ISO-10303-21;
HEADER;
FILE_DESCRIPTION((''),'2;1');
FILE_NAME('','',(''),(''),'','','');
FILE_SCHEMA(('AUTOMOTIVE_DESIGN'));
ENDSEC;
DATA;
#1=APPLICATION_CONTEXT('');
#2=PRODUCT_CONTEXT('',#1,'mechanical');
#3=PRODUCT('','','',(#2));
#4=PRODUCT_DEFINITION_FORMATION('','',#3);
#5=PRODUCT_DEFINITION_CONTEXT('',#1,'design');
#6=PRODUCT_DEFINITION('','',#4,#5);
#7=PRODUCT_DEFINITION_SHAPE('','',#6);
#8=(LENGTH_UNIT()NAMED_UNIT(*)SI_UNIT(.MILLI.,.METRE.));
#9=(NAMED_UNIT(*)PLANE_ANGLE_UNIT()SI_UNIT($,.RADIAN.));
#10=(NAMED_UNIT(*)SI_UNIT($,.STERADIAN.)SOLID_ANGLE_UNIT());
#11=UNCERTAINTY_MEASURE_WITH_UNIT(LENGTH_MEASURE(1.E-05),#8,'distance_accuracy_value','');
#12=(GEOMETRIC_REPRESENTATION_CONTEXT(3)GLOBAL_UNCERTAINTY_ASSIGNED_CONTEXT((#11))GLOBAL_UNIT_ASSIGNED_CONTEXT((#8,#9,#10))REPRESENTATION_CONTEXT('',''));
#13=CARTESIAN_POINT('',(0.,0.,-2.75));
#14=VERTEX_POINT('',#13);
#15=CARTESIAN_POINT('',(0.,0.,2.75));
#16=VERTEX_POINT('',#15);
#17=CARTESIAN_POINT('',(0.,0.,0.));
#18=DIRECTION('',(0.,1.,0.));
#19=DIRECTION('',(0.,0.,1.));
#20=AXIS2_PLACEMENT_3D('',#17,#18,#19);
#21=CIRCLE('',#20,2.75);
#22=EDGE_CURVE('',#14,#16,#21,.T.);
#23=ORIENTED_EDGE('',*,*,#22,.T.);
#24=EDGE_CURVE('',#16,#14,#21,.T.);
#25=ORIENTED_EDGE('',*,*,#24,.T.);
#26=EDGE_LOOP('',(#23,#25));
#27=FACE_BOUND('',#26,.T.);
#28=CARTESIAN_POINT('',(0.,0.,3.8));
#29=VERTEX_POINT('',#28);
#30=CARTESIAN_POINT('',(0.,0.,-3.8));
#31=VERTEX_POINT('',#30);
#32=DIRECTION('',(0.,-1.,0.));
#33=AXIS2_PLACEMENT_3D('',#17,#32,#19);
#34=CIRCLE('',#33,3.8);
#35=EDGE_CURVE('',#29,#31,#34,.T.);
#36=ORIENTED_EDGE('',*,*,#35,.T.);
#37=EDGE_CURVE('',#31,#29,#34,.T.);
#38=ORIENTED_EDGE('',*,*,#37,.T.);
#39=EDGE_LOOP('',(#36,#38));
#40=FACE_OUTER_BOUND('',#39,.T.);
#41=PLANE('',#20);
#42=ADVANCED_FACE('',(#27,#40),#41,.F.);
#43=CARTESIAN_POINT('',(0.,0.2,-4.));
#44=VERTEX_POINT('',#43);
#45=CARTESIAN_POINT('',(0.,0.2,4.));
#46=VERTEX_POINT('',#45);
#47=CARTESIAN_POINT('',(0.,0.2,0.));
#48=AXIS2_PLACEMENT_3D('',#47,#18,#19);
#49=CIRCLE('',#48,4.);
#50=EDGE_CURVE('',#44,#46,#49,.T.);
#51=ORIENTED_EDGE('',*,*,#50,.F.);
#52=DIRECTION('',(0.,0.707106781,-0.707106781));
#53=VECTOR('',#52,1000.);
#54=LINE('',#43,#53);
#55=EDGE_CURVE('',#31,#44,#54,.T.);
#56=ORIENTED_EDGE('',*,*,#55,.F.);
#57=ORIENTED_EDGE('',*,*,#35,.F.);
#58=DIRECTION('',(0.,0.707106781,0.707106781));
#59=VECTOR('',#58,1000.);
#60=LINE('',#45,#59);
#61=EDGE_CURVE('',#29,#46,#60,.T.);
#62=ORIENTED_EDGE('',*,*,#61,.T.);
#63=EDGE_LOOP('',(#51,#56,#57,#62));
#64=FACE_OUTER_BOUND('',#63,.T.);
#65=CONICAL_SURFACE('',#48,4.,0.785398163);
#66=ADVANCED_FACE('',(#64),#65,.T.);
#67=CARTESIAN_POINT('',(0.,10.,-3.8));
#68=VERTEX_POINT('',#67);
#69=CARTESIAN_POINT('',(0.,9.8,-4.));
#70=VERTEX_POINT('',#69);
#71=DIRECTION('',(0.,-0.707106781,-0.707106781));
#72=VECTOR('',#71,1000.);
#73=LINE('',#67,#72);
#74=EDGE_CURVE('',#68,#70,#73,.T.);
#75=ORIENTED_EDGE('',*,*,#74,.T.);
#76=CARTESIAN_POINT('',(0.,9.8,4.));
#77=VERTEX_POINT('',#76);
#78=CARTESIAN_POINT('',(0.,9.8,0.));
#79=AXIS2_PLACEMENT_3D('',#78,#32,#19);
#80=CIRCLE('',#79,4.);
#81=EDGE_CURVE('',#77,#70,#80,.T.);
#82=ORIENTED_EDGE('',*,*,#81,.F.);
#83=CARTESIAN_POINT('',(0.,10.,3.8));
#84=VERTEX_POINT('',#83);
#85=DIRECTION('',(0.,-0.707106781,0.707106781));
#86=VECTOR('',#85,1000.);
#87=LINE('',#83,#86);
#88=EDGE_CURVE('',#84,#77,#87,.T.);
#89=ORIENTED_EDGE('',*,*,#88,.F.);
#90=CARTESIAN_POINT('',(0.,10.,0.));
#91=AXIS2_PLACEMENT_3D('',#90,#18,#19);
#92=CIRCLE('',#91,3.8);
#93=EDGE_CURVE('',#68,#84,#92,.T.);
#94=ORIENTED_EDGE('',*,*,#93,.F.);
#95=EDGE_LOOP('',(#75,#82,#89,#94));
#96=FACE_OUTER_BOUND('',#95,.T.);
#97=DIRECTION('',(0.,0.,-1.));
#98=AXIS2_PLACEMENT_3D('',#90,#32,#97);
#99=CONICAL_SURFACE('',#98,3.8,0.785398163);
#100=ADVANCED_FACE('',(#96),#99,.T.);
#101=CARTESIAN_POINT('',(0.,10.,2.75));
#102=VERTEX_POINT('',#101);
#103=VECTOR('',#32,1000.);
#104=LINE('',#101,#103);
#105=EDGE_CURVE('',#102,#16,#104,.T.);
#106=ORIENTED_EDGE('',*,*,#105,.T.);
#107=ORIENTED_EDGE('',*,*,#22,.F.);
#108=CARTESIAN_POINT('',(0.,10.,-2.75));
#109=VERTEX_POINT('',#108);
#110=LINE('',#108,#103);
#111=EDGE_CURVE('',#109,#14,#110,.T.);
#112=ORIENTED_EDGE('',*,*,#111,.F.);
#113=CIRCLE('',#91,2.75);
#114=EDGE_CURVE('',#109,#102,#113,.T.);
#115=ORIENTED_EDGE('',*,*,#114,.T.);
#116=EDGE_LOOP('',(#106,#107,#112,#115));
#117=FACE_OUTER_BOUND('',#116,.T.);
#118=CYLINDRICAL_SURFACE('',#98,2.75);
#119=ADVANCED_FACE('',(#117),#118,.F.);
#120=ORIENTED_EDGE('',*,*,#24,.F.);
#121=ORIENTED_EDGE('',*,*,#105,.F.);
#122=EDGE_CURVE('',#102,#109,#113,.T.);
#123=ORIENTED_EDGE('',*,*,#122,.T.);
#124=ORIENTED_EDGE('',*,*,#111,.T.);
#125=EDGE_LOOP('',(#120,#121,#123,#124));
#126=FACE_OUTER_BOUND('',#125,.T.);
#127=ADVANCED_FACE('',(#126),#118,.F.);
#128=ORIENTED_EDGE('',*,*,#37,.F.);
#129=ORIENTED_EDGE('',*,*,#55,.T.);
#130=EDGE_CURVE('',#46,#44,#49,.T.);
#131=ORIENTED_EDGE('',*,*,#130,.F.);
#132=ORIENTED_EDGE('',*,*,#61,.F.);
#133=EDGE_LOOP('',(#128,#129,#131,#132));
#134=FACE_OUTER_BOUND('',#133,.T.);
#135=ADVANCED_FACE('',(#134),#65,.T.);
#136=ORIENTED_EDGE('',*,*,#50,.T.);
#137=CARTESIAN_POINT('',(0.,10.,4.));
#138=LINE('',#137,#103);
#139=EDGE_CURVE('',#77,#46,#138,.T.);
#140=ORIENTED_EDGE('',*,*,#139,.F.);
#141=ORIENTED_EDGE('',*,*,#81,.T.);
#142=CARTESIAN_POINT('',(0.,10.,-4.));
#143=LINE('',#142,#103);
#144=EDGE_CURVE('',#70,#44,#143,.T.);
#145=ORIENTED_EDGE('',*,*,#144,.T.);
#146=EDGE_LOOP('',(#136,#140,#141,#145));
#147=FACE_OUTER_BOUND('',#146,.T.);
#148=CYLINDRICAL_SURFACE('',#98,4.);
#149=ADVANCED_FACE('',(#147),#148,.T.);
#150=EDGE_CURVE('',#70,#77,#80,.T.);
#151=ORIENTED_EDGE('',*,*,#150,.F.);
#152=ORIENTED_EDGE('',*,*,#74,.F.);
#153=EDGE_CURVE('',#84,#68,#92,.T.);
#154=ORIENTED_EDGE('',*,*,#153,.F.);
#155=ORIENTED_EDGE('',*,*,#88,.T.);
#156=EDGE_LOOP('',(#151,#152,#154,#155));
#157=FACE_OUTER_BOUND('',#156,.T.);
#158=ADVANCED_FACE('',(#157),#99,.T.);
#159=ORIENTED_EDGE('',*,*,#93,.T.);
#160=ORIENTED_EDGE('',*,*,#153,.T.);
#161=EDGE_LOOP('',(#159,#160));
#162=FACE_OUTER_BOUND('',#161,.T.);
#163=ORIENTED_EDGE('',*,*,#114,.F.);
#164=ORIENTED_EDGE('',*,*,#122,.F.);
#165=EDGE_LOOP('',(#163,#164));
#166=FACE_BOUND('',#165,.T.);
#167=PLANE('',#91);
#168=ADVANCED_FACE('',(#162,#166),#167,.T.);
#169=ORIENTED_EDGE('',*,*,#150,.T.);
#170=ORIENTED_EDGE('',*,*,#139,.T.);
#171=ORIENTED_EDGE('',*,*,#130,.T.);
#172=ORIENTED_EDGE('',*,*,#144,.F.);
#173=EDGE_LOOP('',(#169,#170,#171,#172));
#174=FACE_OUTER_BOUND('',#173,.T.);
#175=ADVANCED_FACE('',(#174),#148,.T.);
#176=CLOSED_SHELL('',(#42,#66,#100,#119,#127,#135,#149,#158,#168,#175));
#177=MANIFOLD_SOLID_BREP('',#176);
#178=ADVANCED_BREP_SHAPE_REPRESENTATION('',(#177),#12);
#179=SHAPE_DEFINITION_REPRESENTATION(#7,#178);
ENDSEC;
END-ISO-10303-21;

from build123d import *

# Parameters (mm, degrees)
SKETCH1_R           = 4
SKETCH1_R_2         = 2.75
BOSS_EXTRUDE1_DEPTH = 10
CHAMFER1_SIZE       = 0.2


with BuildPart() as part:
    # Sketch1 → Boss-Extrude1 (new body)
    with BuildSketch(Plane(origin=(0, 0, 0), x_dir=(1, 0, 0), z_dir=(0, 1, 0))):
        with Locations(Location((0, 0, 0), (0, 0, 270))):
            Circle(SKETCH1_R)
        with Locations(Location((0, 0, 0), (0, 0, 270))):
            Circle(SKETCH1_R_2, mode=Mode.SUBTRACT)
    extrude(amount=BOSS_EXTRUDE1_DEPTH)

    # Chamfer1
    chamfer1_edges = [part.edges().sort_by_distance(p)[0] for p in [
        (0, 0, -4),
        (0, 10, -4),
    ]]
    chamfer(chamfer1_edges, length=CHAMFER1_SIZE)


solid = part.part
